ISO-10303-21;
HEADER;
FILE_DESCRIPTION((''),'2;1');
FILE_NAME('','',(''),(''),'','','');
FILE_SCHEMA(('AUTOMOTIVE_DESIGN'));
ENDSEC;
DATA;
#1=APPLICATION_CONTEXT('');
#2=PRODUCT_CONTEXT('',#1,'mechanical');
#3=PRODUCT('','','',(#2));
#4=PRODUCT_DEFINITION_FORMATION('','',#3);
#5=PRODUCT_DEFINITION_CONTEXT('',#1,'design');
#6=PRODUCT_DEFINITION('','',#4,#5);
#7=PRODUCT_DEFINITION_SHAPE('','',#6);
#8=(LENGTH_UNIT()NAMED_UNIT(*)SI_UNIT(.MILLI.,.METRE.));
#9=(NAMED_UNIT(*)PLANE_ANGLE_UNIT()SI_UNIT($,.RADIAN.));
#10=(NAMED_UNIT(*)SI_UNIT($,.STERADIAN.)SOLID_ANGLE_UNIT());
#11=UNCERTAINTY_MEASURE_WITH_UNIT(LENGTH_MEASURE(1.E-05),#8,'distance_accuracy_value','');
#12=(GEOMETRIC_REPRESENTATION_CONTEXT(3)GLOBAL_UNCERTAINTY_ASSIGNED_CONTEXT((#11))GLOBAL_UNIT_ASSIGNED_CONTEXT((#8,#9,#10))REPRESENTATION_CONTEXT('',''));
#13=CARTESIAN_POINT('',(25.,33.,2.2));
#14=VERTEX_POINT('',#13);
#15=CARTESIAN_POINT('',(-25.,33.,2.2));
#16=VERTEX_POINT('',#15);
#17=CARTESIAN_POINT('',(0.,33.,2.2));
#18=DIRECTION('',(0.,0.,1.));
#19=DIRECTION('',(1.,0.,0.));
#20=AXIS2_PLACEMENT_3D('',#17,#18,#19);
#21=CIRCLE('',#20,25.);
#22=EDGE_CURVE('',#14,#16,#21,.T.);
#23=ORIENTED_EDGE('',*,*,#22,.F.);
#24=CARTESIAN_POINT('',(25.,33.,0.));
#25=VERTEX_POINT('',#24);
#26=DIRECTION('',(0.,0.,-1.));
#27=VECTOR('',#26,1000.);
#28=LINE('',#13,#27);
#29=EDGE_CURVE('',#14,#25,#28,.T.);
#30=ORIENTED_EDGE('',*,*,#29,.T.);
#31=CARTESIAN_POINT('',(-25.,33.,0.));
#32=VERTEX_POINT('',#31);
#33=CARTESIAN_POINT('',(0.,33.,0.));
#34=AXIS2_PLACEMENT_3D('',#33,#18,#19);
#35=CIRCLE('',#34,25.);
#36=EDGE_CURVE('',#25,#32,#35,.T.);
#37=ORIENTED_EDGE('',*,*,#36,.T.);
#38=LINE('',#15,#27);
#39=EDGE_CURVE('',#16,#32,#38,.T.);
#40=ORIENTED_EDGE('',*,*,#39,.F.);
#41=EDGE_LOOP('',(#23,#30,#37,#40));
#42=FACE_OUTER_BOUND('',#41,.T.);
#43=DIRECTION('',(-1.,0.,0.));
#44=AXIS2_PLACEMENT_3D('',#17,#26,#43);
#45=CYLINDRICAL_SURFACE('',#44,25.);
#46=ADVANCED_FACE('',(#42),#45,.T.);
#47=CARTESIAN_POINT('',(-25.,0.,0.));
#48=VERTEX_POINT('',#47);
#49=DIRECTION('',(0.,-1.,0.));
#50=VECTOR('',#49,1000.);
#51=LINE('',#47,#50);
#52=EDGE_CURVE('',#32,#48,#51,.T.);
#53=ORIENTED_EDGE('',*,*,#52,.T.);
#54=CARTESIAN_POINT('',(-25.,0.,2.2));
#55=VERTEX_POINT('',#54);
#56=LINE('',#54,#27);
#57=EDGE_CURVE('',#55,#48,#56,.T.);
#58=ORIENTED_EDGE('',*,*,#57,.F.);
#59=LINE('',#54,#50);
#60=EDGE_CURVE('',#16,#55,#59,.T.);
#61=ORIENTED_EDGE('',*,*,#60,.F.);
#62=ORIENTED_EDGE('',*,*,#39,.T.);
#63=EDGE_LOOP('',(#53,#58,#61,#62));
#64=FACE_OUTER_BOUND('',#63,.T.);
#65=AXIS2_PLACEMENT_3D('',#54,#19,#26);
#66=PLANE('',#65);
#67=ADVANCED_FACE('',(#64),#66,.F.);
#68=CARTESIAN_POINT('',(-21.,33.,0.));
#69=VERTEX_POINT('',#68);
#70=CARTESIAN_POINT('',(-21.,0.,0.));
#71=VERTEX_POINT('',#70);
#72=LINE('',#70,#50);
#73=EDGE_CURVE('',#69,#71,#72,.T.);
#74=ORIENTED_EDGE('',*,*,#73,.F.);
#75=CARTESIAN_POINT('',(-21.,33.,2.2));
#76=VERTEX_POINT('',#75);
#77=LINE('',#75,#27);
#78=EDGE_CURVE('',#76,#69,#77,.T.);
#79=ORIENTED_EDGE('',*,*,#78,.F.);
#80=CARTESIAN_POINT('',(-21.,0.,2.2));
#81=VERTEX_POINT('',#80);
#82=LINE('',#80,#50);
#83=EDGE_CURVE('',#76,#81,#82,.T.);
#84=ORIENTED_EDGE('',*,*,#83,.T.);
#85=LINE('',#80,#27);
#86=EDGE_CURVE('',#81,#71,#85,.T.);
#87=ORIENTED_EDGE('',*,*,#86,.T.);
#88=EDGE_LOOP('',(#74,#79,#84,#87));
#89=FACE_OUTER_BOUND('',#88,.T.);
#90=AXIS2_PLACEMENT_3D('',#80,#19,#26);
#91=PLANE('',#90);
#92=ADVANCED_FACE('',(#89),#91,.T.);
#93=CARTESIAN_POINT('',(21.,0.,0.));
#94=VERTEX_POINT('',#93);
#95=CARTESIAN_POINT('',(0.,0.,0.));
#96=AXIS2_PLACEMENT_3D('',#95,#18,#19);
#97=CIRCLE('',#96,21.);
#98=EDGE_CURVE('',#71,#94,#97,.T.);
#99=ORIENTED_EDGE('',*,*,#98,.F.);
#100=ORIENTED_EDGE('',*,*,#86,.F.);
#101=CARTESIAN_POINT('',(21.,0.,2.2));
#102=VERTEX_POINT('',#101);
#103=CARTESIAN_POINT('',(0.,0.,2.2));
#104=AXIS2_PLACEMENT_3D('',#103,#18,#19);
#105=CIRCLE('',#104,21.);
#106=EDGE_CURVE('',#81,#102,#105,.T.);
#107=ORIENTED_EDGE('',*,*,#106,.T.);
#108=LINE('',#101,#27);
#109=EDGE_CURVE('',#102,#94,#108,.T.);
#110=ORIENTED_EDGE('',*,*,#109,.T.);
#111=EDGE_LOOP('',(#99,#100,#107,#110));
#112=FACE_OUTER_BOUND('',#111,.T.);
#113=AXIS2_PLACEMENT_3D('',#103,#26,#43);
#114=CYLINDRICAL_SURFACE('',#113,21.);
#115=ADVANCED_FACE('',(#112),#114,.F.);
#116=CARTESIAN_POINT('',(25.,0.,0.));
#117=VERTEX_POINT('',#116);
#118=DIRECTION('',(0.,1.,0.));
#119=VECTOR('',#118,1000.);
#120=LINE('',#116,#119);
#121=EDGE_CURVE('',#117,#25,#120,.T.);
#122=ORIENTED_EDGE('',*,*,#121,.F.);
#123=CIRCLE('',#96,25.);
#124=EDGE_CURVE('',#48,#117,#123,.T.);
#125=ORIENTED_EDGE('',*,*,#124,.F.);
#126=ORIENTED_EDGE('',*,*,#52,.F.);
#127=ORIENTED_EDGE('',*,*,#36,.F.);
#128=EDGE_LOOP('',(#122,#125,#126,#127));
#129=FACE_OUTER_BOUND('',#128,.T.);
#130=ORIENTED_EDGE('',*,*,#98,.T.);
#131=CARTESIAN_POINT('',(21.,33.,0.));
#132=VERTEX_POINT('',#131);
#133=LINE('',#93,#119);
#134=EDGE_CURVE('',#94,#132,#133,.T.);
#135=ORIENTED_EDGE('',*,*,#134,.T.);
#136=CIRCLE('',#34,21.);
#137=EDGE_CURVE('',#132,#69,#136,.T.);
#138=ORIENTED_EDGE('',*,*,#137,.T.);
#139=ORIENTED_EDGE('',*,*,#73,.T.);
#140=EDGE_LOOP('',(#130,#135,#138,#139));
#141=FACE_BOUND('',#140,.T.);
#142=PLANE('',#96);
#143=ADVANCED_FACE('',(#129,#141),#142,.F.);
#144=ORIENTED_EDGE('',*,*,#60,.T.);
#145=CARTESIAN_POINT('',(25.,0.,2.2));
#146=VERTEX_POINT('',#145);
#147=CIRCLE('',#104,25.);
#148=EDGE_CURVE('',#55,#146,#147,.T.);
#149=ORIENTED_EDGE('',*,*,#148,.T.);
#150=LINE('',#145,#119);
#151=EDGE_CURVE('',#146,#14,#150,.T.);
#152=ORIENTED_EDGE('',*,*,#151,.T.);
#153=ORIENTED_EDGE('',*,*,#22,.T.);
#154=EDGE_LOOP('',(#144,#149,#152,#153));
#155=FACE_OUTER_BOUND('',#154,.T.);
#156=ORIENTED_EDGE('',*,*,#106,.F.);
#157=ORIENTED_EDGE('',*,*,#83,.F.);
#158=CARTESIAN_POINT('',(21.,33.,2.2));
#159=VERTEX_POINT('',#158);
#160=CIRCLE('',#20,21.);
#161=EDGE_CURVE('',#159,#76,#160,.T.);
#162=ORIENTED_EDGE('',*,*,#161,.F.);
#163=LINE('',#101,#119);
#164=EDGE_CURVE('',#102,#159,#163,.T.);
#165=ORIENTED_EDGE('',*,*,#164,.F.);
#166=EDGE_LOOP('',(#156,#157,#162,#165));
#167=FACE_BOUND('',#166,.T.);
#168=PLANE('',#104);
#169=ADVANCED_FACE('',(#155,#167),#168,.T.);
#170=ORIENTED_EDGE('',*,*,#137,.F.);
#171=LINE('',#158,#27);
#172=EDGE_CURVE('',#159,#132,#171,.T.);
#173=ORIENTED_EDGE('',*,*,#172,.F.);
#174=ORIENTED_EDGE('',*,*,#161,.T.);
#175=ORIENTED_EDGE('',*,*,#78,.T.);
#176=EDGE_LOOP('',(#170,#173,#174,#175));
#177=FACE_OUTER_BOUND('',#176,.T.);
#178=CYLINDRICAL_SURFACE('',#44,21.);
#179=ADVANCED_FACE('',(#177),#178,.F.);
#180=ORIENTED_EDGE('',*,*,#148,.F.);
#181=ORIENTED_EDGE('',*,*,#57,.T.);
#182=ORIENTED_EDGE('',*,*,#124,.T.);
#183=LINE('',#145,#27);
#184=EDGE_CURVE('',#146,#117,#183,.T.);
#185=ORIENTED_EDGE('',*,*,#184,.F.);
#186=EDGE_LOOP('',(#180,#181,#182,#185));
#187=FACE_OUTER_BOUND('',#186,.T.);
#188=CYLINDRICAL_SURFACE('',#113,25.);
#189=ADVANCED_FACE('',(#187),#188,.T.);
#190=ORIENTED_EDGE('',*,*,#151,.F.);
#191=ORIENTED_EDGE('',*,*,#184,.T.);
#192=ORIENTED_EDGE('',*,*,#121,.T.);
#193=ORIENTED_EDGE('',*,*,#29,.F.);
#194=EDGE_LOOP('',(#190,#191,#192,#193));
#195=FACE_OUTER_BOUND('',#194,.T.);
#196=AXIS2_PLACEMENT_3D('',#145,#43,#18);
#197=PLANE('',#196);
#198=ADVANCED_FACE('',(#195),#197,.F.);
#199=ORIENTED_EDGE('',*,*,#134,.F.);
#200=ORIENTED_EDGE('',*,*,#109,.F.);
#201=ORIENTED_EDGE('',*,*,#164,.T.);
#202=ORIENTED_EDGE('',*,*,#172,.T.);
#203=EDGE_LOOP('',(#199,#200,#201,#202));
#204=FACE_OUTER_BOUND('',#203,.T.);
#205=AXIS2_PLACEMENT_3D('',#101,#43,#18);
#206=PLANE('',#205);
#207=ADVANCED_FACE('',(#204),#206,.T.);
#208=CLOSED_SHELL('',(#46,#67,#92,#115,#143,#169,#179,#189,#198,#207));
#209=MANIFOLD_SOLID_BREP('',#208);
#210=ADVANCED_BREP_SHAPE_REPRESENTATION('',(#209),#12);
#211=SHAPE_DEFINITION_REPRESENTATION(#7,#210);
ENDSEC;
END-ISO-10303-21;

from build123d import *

# Parameters (mm, degrees)
BOSS_EXTRUDE1_DEPTH = 2.2


with BuildPart() as part:
    # Sketch1 → Boss-Extrude1 (new body)
    with BuildSketch(Plane.XY):
        with BuildLine():
            Line((-25, 0), (-25, 33))
            ThreePointArc((-25, 33), (0, 58), (25, 33))
            Line((25, 33), (25, 0))
            ThreePointArc((25, 0), (0, -25), (-25, 0))
        make_face()
        with BuildLine():
            Line((-21, 0), (-21, 33))
            ThreePointArc((-21, 33), (0, 54), (21, 33))
            Line((21, 33), (21, 0))
            ThreePointArc((21, 0), (0, -21), (-21, 0))
        make_face(mode=Mode.SUBTRACT)
    extrude(amount=BOSS_EXTRUDE1_DEPTH)


solid = part.part
